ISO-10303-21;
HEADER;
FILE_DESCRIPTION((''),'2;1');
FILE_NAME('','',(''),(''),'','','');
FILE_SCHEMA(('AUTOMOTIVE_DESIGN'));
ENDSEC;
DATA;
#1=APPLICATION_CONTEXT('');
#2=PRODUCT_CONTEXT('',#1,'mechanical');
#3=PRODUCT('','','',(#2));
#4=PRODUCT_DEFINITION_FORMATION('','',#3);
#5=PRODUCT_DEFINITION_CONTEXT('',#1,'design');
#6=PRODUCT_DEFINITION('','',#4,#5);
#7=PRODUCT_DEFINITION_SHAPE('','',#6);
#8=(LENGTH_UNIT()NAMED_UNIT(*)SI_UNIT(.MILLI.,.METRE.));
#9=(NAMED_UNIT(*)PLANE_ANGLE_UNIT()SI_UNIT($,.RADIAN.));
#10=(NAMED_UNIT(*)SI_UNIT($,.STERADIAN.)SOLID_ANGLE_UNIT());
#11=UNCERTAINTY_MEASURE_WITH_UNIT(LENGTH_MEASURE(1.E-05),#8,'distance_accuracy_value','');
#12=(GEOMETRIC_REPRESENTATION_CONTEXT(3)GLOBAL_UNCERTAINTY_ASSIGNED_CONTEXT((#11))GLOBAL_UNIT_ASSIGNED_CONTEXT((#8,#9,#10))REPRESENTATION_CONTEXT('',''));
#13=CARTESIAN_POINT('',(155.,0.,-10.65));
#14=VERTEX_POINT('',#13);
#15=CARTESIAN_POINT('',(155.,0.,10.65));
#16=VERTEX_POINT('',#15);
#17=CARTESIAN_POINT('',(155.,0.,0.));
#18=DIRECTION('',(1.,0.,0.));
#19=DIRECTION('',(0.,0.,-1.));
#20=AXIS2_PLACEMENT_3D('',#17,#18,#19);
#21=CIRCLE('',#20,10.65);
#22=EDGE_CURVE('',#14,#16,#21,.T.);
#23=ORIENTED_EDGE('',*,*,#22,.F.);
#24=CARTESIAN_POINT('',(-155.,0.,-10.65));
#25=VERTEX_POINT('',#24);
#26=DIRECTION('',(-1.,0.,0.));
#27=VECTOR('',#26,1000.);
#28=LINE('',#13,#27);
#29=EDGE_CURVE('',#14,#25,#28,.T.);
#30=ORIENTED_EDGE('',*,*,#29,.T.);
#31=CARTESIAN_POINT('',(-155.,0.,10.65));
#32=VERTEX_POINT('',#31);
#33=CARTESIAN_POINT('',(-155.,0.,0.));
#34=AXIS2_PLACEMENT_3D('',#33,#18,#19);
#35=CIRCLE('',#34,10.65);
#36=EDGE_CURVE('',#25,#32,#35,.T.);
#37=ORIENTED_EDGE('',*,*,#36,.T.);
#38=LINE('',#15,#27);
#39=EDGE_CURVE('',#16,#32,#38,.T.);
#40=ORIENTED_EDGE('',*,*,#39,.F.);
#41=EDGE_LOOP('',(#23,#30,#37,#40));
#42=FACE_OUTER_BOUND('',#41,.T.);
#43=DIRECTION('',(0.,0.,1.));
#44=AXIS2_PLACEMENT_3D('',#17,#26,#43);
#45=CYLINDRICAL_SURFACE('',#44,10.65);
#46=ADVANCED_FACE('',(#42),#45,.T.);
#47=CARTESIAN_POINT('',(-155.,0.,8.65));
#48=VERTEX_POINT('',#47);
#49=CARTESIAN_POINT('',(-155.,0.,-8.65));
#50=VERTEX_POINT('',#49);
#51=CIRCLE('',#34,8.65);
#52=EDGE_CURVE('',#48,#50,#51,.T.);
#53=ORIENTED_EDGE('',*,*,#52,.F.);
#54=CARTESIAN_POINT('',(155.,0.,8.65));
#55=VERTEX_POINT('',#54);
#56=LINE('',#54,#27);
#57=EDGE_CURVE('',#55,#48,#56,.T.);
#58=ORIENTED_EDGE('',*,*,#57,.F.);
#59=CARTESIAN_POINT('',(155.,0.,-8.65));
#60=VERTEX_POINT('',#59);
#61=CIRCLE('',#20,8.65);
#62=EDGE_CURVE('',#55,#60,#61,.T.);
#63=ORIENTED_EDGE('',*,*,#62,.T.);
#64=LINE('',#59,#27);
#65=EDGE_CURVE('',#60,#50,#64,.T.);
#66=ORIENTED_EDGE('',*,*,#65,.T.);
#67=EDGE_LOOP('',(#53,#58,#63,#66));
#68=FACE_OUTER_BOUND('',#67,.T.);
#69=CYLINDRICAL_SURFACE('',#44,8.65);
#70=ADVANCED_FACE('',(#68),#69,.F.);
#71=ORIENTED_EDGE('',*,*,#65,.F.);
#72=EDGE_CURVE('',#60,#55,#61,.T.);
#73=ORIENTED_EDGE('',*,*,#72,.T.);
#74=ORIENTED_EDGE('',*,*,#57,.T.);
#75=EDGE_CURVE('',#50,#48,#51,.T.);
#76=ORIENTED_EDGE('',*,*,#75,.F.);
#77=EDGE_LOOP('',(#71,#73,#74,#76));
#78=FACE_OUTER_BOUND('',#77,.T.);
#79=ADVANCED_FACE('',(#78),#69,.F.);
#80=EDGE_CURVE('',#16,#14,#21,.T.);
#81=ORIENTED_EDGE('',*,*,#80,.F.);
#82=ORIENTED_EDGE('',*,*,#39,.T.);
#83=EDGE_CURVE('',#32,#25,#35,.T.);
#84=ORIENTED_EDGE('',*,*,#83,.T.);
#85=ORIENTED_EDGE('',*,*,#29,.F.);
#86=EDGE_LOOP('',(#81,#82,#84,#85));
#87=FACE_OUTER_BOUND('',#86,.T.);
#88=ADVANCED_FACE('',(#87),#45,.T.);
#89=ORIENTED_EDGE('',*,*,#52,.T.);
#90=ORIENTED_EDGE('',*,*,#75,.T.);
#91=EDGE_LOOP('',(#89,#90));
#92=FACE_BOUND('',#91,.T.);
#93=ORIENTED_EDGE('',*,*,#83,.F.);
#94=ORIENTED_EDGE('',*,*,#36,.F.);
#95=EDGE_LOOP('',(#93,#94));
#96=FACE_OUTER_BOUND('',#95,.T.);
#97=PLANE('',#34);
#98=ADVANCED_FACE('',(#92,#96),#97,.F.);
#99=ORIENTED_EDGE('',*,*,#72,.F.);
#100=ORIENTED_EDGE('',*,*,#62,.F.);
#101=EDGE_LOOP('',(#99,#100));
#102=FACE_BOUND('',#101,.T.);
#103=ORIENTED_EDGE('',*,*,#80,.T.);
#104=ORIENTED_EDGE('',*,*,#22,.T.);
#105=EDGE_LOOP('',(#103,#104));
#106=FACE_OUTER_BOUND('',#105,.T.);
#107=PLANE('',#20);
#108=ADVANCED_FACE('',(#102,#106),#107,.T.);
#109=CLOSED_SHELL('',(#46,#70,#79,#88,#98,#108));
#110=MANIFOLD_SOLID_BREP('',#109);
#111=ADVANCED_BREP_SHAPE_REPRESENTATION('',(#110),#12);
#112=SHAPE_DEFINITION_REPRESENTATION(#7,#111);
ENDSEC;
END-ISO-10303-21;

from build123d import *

# Parameters (mm, degrees)
SKETCH1_R                                  = 10.65
SKETCH1_R_2                                = 8.65
GB_T6728_2002_ROUND_TUBE_021_3_X_2_1_DEPTH = 310


with BuildPart() as part:
    # Sketch1 → Gb／t6728-2002 round tube 021.3 X 2 (1) (new body)
    with BuildSketch(Plane(origin=(-155, 0, 0), x_dir=(0, 0, -1), z_dir=(1, 0, 0))):
        Circle(SKETCH1_R)
        Circle(SKETCH1_R_2, mode=Mode.SUBTRACT)
    extrude(amount=GB_T6728_2002_ROUND_TUBE_021_3_X_2_1_DEPTH)


solid = part.part
